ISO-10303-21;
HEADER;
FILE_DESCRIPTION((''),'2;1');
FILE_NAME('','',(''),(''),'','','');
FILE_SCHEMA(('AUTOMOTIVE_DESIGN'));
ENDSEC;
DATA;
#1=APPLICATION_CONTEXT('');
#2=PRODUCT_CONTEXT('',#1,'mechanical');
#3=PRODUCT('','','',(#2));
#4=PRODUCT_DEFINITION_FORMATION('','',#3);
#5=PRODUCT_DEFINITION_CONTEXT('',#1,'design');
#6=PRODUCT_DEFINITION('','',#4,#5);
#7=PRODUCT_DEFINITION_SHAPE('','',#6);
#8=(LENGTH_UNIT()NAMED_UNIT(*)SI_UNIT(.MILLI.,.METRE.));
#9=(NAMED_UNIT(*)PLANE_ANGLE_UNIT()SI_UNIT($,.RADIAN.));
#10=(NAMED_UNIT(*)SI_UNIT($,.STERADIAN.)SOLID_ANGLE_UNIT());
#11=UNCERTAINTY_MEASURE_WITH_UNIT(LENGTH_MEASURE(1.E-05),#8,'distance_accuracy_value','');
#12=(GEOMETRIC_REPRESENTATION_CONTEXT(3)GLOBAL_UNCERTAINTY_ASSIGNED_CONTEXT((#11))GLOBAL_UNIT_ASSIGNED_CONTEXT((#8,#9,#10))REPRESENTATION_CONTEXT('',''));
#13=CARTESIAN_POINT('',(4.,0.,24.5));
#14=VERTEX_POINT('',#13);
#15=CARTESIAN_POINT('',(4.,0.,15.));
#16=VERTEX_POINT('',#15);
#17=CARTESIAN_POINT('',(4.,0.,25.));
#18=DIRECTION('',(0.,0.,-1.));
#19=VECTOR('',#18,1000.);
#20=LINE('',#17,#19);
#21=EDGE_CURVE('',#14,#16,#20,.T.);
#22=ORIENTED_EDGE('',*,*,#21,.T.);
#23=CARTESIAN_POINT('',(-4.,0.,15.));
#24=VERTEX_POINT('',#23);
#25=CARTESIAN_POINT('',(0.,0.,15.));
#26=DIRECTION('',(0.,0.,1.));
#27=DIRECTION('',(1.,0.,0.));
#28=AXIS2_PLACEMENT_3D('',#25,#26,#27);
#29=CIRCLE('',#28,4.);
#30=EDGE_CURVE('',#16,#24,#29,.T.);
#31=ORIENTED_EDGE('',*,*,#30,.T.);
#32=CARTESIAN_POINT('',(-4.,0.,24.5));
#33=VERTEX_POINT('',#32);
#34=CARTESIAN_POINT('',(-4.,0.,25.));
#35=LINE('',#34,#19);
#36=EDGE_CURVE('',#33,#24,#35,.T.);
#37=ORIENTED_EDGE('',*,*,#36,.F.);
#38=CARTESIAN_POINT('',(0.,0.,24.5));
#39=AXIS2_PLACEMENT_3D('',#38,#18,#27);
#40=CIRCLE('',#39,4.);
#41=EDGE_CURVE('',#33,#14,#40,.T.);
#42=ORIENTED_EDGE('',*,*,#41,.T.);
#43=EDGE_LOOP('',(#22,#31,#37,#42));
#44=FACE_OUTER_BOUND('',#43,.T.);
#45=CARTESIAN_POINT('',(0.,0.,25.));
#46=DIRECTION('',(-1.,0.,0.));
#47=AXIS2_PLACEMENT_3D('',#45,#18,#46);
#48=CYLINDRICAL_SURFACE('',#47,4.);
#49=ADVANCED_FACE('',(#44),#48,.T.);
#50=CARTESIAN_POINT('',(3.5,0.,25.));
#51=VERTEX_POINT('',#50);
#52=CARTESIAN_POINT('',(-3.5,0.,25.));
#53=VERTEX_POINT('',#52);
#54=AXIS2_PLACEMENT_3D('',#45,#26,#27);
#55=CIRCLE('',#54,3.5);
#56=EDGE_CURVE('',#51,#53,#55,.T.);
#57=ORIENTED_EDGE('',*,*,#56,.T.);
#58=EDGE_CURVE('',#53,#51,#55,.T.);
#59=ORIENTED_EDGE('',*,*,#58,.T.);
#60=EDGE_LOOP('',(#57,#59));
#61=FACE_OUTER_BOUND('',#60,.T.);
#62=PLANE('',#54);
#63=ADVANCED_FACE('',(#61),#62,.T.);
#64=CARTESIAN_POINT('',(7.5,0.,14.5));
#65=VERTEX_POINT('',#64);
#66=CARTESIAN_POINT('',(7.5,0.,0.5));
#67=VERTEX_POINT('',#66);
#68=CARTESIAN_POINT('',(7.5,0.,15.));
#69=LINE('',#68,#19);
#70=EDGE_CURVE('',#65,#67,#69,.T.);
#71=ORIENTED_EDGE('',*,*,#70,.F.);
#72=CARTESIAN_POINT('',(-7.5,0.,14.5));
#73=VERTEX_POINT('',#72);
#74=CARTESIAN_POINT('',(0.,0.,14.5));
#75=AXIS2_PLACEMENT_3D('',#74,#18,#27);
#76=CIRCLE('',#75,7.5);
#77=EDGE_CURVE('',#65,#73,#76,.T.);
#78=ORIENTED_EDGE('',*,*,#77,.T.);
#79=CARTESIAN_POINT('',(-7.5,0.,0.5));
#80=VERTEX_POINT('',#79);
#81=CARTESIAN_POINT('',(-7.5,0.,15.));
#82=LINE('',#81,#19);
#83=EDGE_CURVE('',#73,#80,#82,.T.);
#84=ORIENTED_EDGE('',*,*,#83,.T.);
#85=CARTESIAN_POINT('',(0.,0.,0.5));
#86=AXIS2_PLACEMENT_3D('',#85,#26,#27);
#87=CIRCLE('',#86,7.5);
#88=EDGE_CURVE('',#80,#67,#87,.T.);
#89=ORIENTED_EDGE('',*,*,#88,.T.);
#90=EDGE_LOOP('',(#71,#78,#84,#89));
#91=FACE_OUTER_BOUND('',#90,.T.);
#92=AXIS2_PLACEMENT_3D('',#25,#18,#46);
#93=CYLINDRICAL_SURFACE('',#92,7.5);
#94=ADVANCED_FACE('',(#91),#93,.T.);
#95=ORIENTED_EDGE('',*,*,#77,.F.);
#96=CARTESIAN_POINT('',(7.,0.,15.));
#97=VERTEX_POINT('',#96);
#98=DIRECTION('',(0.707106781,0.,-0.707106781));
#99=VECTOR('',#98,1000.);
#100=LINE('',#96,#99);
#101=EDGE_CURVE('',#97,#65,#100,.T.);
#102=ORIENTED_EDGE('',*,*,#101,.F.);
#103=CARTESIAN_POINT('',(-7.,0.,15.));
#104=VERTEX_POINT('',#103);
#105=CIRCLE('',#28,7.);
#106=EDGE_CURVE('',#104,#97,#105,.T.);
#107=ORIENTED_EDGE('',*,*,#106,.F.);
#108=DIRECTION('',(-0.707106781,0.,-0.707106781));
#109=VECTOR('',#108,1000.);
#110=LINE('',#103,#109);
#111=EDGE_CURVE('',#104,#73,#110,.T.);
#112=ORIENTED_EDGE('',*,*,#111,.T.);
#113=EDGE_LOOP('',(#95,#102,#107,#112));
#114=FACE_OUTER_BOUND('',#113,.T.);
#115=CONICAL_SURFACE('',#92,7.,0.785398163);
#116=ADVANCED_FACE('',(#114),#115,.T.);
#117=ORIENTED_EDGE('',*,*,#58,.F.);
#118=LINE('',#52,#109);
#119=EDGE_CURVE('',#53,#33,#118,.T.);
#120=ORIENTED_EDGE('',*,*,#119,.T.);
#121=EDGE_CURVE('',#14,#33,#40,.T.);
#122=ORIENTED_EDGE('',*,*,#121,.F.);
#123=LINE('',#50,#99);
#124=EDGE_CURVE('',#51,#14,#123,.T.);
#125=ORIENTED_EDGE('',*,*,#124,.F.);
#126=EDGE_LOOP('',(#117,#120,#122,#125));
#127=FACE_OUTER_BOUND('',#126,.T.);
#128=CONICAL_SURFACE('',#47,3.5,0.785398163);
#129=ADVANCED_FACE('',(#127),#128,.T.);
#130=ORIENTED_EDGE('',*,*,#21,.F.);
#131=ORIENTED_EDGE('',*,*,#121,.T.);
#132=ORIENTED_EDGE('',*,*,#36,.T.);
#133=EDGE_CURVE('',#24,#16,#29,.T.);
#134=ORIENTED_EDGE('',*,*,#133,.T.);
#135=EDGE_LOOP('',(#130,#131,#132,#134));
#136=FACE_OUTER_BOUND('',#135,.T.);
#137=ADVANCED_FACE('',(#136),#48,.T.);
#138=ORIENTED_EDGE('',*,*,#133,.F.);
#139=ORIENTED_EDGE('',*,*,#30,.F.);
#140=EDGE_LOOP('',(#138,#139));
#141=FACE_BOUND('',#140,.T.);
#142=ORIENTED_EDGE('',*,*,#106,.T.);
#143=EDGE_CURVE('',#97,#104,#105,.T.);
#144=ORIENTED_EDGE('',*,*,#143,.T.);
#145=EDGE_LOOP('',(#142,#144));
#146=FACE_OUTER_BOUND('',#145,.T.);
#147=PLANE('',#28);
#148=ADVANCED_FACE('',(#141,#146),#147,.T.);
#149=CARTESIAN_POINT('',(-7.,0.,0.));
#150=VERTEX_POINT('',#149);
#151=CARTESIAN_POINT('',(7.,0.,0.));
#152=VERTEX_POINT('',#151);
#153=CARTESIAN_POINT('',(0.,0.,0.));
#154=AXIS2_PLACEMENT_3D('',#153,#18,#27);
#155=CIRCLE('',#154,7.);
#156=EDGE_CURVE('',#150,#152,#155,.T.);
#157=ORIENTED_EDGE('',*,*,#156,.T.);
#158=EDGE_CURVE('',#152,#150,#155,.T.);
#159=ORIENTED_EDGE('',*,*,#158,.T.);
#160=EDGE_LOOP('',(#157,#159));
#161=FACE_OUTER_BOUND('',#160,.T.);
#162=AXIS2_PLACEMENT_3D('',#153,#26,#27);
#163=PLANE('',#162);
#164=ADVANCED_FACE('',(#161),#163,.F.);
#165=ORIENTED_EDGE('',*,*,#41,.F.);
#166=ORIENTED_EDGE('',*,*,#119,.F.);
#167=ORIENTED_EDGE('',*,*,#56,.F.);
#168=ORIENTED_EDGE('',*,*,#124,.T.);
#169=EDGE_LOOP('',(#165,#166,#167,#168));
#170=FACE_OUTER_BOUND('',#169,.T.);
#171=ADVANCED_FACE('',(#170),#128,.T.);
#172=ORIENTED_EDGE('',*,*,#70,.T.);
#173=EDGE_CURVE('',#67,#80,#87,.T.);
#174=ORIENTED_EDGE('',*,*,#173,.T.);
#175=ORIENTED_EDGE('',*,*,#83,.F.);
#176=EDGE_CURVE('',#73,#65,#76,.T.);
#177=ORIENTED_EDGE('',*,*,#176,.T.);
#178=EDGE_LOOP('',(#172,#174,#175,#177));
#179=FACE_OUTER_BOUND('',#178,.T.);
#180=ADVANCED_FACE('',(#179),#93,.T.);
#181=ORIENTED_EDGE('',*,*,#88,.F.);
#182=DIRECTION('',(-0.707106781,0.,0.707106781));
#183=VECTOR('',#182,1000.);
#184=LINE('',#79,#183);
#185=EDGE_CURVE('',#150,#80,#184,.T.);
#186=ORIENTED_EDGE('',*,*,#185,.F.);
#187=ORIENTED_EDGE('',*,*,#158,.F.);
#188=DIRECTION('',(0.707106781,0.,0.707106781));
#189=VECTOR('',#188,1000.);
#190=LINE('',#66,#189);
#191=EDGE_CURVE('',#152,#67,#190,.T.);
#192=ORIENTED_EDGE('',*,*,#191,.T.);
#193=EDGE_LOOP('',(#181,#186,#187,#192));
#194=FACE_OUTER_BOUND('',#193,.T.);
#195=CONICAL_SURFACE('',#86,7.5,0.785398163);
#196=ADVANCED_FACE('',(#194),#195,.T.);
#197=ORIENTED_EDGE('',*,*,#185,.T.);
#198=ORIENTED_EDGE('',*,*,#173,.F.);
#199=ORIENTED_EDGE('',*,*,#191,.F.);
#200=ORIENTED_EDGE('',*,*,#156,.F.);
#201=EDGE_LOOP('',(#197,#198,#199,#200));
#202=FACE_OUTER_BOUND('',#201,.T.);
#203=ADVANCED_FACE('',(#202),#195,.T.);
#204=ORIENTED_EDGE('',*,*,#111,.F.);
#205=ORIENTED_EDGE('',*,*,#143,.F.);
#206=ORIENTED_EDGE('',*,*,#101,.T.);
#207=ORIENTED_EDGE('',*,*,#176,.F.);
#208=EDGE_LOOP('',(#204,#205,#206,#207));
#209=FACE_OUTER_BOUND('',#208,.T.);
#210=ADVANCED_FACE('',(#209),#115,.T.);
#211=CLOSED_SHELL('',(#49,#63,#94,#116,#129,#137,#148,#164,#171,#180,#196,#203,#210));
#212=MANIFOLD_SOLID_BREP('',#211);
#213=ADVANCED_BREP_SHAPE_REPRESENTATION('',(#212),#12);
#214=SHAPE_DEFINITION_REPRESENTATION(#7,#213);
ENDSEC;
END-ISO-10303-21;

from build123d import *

# Parameters (mm, degrees)
SKETCH1_R           = 7.5
BOSS_EXTRUDE1_DEPTH = 15
SKETCH2_R           = 4
BOSS_EXTRUDE2_DEPTH = 10
CHAMFER1_SIZE       = 0.5


with BuildPart() as part:
    # Sketch1 → Boss-Extrude1 (new body)
    with BuildSketch(Plane.XY):
        Circle(SKETCH1_R)
    extrude(amount=BOSS_EXTRUDE1_DEPTH)

    # Sketch2 → Boss-Extrude2 (add)
    with BuildSketch(Plane.XY.offset(15)):
        Circle(SKETCH2_R)
    extrude(amount=BOSS_EXTRUDE2_DEPTH)

    # Chamfer1
    chamfer1_edges = [part.edges().sort_by_distance(p)[0] for p in [
        (-7.5, 0, 0),
        (-7.5, 0, 15),
        (-4, 0, 25),
    ]]
    chamfer(chamfer1_edges, length=CHAMFER1_SIZE)


solid = part.part
